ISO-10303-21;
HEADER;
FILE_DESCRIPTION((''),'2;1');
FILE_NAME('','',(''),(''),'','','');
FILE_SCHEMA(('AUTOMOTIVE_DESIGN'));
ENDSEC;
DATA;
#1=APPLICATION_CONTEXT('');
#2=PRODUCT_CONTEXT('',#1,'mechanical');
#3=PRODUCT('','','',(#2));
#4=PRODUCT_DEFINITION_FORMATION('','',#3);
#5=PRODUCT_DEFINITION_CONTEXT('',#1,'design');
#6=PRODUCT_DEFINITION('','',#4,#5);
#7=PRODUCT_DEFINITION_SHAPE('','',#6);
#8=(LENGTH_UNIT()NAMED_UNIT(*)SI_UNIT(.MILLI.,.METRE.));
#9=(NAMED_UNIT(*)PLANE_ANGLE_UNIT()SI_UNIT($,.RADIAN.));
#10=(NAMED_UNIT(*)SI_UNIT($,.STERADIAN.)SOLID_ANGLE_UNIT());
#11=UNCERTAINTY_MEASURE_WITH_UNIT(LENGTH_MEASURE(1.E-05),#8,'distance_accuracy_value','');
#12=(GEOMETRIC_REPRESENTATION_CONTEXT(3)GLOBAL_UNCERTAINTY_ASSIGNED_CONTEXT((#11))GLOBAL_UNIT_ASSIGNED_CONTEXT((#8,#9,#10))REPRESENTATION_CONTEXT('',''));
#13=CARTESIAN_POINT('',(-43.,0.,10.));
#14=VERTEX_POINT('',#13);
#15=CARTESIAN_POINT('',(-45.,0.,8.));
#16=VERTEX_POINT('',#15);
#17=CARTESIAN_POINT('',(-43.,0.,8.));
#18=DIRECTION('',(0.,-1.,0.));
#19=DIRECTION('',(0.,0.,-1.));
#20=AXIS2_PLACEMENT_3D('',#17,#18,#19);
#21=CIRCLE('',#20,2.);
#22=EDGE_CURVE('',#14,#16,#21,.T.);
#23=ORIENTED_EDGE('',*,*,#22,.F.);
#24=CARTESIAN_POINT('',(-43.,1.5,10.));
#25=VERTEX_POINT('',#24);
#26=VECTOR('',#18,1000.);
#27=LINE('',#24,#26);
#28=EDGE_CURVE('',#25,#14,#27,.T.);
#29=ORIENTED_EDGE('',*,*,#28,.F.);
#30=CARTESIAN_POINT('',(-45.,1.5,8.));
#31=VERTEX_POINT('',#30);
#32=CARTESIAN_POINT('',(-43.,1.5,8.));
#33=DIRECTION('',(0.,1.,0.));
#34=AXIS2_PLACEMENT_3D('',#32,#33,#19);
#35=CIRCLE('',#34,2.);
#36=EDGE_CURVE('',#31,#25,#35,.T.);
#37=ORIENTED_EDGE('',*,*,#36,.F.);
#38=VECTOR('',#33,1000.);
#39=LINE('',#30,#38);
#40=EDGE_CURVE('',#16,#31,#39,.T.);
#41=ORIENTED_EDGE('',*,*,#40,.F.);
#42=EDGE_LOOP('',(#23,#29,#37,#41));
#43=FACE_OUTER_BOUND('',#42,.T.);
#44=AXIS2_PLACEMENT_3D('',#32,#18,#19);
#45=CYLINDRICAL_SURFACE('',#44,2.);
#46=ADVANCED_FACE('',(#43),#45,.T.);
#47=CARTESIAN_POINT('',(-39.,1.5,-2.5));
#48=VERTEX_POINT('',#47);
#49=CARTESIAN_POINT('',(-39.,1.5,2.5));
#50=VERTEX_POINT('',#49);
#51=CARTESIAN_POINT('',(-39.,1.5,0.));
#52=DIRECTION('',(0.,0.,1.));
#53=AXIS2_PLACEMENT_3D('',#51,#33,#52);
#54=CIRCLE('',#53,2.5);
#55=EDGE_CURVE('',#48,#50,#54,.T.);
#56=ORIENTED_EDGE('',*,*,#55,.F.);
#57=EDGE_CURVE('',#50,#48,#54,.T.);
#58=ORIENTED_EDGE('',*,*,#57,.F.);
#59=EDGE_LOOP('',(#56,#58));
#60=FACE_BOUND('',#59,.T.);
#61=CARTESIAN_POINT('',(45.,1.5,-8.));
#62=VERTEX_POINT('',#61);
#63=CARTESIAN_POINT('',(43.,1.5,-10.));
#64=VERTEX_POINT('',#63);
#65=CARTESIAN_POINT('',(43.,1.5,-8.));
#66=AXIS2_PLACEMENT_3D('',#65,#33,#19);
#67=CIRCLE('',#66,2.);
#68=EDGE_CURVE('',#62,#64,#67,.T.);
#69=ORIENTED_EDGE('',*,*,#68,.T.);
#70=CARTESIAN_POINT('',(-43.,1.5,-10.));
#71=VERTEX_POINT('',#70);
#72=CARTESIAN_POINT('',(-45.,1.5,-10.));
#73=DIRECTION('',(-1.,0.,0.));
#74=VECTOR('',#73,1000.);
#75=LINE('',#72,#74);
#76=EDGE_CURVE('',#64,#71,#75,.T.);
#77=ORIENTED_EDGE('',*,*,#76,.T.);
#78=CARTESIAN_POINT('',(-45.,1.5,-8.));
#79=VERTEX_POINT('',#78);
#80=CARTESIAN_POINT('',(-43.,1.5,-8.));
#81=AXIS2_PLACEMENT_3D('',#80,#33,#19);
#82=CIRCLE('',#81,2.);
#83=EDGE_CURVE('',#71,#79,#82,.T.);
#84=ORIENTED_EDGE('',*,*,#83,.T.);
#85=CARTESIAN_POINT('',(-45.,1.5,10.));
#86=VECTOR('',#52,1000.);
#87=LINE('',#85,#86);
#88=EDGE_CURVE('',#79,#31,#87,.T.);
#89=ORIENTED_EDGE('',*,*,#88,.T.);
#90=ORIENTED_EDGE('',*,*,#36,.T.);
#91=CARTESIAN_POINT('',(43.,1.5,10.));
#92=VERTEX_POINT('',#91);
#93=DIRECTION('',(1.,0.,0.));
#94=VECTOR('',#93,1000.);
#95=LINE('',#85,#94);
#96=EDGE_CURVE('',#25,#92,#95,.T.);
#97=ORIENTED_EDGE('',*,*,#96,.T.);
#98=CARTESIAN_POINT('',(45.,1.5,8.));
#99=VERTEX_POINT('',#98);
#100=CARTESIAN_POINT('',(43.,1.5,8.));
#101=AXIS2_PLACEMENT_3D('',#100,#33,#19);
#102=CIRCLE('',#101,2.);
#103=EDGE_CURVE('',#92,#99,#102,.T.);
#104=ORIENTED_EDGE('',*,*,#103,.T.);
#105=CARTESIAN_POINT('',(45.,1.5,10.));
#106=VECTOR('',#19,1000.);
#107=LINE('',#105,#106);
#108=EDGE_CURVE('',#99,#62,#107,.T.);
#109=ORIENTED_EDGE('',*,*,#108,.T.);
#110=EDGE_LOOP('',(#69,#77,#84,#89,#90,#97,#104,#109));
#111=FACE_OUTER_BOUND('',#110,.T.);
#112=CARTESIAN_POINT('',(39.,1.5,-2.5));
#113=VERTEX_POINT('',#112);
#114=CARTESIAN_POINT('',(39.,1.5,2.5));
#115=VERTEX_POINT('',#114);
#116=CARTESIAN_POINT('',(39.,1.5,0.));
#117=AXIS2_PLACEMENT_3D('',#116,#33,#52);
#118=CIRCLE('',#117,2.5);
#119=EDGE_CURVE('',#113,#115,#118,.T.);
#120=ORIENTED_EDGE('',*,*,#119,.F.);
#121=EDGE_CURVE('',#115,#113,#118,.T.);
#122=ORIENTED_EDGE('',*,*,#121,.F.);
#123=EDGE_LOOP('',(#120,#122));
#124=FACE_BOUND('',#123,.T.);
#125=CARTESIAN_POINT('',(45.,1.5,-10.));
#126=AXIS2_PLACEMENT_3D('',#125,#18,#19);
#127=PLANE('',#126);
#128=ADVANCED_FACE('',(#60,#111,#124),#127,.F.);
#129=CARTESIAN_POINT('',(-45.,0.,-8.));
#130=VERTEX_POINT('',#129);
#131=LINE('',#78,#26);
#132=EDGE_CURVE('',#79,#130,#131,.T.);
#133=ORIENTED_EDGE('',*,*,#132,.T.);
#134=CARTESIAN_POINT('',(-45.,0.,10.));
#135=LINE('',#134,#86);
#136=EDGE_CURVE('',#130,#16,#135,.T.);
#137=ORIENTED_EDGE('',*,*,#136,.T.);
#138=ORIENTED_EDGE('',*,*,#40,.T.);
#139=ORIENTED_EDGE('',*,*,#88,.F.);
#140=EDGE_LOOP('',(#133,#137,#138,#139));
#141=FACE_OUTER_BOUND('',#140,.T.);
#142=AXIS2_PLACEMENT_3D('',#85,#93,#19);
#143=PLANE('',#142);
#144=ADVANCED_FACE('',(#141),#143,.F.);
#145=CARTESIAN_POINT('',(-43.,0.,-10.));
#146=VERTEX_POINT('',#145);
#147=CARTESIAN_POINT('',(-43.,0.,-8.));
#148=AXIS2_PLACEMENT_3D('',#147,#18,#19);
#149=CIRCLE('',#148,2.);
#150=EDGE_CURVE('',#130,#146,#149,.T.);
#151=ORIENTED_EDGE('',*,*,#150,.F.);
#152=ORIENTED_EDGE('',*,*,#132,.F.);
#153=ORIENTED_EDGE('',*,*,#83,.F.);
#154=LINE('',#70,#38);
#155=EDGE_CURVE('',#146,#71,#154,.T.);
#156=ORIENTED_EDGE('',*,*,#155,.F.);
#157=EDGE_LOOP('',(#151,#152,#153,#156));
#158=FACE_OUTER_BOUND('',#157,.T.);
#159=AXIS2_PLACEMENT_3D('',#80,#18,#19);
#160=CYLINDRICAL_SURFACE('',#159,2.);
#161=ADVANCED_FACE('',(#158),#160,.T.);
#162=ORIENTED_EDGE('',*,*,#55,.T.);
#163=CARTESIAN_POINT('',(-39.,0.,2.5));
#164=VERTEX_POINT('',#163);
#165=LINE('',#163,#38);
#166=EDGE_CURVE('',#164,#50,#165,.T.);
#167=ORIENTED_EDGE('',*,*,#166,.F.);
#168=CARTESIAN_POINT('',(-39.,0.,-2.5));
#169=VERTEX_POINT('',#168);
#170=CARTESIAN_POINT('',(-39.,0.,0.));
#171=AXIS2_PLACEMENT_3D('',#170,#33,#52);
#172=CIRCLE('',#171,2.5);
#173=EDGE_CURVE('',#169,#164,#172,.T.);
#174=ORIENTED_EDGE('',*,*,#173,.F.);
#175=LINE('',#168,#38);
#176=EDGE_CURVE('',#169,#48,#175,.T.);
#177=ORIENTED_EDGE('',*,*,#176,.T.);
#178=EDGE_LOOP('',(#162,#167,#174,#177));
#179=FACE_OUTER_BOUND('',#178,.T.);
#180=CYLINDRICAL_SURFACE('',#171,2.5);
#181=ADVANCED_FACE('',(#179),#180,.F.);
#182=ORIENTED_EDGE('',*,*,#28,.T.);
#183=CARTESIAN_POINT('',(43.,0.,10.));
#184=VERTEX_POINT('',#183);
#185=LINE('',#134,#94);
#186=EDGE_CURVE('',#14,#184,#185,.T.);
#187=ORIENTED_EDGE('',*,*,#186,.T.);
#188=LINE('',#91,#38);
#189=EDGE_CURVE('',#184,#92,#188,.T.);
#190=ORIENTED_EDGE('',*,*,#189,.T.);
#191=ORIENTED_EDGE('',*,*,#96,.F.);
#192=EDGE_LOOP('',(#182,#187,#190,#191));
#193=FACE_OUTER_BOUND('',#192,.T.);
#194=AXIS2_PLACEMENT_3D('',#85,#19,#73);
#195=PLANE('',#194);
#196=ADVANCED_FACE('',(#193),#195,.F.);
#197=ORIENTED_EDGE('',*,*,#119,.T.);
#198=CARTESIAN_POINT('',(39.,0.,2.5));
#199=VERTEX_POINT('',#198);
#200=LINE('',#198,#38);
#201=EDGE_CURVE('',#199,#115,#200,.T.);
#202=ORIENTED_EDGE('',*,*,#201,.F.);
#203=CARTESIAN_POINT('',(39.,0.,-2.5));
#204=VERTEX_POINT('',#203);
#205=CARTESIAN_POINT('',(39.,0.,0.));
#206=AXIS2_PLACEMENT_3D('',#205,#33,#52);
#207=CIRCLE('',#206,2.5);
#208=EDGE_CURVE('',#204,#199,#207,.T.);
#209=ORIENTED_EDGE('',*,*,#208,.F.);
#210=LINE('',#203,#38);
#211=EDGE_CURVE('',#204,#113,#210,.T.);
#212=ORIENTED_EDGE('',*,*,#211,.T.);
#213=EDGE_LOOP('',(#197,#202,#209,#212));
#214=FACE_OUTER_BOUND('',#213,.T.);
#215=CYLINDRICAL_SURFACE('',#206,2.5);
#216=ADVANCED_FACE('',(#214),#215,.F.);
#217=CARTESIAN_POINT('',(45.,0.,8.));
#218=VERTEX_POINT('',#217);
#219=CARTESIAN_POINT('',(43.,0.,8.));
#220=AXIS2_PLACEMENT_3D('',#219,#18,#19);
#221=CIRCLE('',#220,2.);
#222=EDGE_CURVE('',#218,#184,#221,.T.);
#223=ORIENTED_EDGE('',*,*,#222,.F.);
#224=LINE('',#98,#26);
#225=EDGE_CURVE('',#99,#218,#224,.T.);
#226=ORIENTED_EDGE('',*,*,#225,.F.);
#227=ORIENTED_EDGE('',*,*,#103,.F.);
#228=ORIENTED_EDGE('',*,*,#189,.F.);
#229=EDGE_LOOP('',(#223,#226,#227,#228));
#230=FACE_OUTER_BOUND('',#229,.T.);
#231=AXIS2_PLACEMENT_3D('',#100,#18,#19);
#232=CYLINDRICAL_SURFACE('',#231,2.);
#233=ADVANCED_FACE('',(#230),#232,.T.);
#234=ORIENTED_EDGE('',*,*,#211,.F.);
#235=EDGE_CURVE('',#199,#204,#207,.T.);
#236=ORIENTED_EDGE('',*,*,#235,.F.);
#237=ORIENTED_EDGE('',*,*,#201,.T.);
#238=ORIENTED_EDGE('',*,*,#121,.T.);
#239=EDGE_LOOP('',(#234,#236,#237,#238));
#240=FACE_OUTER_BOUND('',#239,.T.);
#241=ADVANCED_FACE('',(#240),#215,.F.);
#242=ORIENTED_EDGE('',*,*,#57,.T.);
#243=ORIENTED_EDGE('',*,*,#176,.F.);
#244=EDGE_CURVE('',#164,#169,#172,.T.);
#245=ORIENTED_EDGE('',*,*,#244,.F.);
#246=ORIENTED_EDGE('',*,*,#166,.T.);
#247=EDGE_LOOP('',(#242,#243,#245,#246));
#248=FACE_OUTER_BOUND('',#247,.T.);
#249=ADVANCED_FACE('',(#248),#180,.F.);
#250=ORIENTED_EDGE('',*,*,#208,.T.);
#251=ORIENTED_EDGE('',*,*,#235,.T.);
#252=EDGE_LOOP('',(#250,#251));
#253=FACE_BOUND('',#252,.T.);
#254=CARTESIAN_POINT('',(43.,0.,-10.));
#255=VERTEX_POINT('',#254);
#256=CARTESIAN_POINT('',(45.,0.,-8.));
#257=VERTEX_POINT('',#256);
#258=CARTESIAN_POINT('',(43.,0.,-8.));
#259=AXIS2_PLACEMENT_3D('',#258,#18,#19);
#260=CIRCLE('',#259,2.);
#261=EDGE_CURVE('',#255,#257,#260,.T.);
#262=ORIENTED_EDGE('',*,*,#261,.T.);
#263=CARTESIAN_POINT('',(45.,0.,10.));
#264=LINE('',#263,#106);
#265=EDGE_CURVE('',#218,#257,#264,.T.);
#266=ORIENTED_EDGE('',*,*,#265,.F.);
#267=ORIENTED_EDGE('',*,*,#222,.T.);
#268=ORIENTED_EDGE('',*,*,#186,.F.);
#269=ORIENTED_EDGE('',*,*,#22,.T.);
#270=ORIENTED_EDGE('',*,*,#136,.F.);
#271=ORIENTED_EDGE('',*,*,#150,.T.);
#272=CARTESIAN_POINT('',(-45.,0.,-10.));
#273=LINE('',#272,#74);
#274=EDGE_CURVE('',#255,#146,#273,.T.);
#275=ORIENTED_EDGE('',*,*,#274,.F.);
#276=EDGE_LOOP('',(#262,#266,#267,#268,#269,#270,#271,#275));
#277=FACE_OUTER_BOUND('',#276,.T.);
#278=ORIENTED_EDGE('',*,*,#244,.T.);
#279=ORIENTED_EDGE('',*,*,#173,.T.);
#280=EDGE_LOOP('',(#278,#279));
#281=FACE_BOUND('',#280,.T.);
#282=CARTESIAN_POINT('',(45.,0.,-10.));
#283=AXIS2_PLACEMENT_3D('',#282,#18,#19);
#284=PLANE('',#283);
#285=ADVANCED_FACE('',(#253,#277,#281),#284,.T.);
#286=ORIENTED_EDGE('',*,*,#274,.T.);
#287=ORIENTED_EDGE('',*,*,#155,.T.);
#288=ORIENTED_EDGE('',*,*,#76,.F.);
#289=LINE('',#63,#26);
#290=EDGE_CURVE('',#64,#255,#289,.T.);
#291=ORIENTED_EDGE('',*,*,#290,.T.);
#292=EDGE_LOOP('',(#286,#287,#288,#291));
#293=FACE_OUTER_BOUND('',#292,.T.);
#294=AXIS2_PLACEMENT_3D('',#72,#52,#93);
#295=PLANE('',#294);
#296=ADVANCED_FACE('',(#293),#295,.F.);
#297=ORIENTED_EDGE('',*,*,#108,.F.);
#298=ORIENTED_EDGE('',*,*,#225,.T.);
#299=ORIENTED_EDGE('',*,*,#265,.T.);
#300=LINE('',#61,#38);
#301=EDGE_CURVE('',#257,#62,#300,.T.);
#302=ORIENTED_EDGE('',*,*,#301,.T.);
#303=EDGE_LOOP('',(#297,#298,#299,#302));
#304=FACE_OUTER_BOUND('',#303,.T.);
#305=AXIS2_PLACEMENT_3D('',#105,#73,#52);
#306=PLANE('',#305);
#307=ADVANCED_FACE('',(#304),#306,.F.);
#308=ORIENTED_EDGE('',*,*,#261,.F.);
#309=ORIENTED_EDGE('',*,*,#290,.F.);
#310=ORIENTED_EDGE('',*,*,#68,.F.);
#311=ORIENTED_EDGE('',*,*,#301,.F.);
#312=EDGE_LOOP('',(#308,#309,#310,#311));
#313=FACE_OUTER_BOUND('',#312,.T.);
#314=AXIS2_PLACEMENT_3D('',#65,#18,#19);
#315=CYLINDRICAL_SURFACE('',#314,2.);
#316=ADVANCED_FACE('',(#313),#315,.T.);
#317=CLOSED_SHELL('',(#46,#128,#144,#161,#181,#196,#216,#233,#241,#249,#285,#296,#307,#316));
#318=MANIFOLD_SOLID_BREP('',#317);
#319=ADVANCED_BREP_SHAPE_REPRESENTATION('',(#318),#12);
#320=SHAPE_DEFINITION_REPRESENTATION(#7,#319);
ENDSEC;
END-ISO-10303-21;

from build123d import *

# Parameters (mm, degrees)
SKETCH_1_W          = 90
SKETCH_1_H          = 20
EXTRUDE_1_DEPTH     = 1.5
SKETCH_2_R          = 2.5
CUT_EXTRUDE_1_DEPTH = 47.122120506
FILLET_1_R          = 2


with BuildPart() as part:
    # 草图1 → 凸台-拉伸1 (new body)
    with BuildSketch(Plane(origin=(0, 0, 0), x_dir=(1, 0, 0), z_dir=(0, 1, 0))):
        Rectangle(SKETCH_1_W, SKETCH_1_H)
    extrude(amount=EXTRUDE_1_DEPTH)

    # 草图2 → 切除-拉伸1 (cut, through all)
    with BuildSketch(Plane(origin=(0, 1.5, 0), x_dir=(1, 0, 0), z_dir=(0, 1, 0))):
        with Locations(Location((-39, 0, 0), (0, 0, 270))):
            Circle(SKETCH_2_R)
        with Locations(Location((39, 0, 0), (0, 0, 270))):
            Circle(SKETCH_2_R)
    extrude(amount=-CUT_EXTRUDE_1_DEPTH, mode=Mode.SUBTRACT)

    # 圆角1
    fillet_1_edges = [part.edges().sort_by_distance(p)[0] for p in [
        (45, 0.75, 10),
        (-45, 0.75, 10),
        (-45, 0.75, -10),
        (45, 0.75, -10),
    ]]
    fillet(fillet_1_edges, radius=FILLET_1_R)


solid = part.part
